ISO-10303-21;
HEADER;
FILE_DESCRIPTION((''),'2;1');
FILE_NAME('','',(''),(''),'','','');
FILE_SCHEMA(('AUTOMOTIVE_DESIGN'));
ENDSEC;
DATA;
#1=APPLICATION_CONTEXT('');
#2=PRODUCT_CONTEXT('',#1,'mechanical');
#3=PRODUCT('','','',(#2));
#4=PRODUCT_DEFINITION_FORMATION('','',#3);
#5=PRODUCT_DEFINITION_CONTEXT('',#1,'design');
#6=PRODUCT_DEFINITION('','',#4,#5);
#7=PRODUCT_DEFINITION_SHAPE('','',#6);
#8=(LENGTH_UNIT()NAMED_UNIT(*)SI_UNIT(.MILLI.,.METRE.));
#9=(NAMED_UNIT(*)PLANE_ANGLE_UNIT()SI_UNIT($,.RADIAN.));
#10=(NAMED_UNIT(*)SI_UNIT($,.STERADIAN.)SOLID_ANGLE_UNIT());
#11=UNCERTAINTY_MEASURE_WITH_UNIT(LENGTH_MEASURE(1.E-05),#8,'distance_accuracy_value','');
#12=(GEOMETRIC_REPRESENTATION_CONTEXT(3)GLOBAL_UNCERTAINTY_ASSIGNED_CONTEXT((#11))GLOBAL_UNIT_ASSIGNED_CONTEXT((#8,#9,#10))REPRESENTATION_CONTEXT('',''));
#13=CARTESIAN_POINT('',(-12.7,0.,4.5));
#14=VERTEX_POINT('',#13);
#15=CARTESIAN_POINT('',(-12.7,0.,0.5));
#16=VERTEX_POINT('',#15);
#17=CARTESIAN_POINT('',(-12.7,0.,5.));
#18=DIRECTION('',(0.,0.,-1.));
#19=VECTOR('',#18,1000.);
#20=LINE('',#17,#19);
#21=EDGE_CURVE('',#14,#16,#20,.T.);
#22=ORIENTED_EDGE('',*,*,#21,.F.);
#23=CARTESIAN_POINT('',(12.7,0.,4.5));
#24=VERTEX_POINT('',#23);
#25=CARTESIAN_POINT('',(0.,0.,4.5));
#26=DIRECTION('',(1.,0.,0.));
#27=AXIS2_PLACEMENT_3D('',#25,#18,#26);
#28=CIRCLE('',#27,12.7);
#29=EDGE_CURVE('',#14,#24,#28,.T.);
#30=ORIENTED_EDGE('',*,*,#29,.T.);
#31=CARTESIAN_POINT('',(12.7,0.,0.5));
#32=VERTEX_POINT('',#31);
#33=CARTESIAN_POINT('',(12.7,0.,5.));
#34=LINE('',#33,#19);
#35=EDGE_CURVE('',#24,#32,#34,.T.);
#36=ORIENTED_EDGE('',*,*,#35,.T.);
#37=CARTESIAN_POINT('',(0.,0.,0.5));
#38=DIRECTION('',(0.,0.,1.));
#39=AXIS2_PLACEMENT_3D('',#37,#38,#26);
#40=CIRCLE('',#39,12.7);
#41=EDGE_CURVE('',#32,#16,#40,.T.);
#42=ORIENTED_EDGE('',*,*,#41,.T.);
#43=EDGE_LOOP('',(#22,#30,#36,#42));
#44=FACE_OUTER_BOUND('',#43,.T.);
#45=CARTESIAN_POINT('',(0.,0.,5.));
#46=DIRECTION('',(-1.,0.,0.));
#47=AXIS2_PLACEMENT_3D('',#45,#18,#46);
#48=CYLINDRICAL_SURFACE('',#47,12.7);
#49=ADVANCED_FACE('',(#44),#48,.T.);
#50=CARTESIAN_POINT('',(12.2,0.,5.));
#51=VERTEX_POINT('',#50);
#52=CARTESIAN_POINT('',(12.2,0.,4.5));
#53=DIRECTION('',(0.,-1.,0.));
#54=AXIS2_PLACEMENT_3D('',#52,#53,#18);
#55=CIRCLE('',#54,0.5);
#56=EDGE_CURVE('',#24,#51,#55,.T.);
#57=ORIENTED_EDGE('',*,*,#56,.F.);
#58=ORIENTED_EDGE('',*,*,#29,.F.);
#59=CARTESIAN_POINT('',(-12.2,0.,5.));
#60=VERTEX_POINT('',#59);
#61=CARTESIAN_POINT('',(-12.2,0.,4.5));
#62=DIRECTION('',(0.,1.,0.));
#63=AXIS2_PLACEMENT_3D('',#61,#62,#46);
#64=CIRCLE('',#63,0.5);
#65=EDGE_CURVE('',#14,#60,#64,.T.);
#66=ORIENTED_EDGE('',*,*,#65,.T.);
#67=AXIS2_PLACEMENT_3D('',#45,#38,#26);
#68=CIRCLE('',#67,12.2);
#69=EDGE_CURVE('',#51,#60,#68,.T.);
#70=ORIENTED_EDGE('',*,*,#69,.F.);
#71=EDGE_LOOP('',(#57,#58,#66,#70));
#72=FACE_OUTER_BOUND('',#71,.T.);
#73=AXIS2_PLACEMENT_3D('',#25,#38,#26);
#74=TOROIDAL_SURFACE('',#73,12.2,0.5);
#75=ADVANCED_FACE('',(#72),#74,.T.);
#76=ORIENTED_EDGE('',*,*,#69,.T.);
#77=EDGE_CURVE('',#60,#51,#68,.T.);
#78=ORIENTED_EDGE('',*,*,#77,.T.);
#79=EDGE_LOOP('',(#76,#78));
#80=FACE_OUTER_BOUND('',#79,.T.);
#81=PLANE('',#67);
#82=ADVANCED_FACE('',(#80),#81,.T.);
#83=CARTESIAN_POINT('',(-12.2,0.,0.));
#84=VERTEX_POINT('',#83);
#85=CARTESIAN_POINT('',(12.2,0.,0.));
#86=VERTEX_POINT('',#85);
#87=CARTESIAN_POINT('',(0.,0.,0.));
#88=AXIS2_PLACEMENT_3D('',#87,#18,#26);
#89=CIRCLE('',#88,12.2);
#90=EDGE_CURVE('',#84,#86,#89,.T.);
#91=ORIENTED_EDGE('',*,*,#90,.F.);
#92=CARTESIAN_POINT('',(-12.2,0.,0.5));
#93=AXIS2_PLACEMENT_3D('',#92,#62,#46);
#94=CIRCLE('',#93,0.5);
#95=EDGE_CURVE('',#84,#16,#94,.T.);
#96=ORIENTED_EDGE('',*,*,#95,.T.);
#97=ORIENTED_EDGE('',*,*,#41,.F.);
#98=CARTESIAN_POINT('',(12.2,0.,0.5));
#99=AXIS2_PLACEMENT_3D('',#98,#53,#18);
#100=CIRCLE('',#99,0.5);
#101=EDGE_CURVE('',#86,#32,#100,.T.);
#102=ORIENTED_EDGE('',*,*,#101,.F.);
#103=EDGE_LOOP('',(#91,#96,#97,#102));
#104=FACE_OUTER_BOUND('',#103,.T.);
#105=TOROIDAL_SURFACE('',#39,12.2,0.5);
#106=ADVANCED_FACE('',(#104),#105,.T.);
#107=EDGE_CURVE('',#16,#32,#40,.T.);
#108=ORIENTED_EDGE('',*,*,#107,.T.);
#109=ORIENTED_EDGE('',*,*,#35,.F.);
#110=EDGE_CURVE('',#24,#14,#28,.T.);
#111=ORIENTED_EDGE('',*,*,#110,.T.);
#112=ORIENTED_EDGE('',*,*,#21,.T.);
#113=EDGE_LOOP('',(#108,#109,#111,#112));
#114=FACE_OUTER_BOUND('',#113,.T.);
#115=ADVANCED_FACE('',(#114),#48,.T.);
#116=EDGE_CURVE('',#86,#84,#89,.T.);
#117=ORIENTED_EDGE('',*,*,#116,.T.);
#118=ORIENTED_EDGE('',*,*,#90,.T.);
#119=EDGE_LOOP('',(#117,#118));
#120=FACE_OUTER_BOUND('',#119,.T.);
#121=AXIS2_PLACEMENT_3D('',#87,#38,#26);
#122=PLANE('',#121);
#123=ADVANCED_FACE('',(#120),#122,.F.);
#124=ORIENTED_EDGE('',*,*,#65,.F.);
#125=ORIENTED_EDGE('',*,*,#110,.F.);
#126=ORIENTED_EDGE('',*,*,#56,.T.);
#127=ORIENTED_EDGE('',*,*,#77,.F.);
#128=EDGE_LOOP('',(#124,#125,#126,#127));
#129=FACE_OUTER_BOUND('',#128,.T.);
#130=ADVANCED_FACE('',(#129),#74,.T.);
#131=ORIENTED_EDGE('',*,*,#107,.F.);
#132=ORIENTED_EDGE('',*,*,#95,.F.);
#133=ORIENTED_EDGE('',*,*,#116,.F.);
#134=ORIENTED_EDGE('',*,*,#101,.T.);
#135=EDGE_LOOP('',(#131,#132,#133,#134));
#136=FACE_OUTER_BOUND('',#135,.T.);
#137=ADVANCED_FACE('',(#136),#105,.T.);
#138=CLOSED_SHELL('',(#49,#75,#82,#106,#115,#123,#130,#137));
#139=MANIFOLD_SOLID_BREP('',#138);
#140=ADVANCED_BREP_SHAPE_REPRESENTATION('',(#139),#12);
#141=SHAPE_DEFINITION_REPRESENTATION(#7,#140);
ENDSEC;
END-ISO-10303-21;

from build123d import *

# Parameters (mm, degrees)
SKETCH1_R           = 12.7
BOSS_EXTRUDE1_DEPTH = 5
FILLET1_R           = 0.5


with BuildPart() as part:
    # Sketch1 → Boss-Extrude1 (new body)
    with BuildSketch(Plane.XY):
        Circle(SKETCH1_R)
    extrude(amount=BOSS_EXTRUDE1_DEPTH)

    # Fillet1
    fillet1_edges = [part.edges().sort_by_distance(p)[0] for p in [
        (-12.7, 0, 0),
        (-12.7, 0, 5),
    ]]
    fillet(fillet1_edges, radius=FILLET1_R)


solid = part.part
